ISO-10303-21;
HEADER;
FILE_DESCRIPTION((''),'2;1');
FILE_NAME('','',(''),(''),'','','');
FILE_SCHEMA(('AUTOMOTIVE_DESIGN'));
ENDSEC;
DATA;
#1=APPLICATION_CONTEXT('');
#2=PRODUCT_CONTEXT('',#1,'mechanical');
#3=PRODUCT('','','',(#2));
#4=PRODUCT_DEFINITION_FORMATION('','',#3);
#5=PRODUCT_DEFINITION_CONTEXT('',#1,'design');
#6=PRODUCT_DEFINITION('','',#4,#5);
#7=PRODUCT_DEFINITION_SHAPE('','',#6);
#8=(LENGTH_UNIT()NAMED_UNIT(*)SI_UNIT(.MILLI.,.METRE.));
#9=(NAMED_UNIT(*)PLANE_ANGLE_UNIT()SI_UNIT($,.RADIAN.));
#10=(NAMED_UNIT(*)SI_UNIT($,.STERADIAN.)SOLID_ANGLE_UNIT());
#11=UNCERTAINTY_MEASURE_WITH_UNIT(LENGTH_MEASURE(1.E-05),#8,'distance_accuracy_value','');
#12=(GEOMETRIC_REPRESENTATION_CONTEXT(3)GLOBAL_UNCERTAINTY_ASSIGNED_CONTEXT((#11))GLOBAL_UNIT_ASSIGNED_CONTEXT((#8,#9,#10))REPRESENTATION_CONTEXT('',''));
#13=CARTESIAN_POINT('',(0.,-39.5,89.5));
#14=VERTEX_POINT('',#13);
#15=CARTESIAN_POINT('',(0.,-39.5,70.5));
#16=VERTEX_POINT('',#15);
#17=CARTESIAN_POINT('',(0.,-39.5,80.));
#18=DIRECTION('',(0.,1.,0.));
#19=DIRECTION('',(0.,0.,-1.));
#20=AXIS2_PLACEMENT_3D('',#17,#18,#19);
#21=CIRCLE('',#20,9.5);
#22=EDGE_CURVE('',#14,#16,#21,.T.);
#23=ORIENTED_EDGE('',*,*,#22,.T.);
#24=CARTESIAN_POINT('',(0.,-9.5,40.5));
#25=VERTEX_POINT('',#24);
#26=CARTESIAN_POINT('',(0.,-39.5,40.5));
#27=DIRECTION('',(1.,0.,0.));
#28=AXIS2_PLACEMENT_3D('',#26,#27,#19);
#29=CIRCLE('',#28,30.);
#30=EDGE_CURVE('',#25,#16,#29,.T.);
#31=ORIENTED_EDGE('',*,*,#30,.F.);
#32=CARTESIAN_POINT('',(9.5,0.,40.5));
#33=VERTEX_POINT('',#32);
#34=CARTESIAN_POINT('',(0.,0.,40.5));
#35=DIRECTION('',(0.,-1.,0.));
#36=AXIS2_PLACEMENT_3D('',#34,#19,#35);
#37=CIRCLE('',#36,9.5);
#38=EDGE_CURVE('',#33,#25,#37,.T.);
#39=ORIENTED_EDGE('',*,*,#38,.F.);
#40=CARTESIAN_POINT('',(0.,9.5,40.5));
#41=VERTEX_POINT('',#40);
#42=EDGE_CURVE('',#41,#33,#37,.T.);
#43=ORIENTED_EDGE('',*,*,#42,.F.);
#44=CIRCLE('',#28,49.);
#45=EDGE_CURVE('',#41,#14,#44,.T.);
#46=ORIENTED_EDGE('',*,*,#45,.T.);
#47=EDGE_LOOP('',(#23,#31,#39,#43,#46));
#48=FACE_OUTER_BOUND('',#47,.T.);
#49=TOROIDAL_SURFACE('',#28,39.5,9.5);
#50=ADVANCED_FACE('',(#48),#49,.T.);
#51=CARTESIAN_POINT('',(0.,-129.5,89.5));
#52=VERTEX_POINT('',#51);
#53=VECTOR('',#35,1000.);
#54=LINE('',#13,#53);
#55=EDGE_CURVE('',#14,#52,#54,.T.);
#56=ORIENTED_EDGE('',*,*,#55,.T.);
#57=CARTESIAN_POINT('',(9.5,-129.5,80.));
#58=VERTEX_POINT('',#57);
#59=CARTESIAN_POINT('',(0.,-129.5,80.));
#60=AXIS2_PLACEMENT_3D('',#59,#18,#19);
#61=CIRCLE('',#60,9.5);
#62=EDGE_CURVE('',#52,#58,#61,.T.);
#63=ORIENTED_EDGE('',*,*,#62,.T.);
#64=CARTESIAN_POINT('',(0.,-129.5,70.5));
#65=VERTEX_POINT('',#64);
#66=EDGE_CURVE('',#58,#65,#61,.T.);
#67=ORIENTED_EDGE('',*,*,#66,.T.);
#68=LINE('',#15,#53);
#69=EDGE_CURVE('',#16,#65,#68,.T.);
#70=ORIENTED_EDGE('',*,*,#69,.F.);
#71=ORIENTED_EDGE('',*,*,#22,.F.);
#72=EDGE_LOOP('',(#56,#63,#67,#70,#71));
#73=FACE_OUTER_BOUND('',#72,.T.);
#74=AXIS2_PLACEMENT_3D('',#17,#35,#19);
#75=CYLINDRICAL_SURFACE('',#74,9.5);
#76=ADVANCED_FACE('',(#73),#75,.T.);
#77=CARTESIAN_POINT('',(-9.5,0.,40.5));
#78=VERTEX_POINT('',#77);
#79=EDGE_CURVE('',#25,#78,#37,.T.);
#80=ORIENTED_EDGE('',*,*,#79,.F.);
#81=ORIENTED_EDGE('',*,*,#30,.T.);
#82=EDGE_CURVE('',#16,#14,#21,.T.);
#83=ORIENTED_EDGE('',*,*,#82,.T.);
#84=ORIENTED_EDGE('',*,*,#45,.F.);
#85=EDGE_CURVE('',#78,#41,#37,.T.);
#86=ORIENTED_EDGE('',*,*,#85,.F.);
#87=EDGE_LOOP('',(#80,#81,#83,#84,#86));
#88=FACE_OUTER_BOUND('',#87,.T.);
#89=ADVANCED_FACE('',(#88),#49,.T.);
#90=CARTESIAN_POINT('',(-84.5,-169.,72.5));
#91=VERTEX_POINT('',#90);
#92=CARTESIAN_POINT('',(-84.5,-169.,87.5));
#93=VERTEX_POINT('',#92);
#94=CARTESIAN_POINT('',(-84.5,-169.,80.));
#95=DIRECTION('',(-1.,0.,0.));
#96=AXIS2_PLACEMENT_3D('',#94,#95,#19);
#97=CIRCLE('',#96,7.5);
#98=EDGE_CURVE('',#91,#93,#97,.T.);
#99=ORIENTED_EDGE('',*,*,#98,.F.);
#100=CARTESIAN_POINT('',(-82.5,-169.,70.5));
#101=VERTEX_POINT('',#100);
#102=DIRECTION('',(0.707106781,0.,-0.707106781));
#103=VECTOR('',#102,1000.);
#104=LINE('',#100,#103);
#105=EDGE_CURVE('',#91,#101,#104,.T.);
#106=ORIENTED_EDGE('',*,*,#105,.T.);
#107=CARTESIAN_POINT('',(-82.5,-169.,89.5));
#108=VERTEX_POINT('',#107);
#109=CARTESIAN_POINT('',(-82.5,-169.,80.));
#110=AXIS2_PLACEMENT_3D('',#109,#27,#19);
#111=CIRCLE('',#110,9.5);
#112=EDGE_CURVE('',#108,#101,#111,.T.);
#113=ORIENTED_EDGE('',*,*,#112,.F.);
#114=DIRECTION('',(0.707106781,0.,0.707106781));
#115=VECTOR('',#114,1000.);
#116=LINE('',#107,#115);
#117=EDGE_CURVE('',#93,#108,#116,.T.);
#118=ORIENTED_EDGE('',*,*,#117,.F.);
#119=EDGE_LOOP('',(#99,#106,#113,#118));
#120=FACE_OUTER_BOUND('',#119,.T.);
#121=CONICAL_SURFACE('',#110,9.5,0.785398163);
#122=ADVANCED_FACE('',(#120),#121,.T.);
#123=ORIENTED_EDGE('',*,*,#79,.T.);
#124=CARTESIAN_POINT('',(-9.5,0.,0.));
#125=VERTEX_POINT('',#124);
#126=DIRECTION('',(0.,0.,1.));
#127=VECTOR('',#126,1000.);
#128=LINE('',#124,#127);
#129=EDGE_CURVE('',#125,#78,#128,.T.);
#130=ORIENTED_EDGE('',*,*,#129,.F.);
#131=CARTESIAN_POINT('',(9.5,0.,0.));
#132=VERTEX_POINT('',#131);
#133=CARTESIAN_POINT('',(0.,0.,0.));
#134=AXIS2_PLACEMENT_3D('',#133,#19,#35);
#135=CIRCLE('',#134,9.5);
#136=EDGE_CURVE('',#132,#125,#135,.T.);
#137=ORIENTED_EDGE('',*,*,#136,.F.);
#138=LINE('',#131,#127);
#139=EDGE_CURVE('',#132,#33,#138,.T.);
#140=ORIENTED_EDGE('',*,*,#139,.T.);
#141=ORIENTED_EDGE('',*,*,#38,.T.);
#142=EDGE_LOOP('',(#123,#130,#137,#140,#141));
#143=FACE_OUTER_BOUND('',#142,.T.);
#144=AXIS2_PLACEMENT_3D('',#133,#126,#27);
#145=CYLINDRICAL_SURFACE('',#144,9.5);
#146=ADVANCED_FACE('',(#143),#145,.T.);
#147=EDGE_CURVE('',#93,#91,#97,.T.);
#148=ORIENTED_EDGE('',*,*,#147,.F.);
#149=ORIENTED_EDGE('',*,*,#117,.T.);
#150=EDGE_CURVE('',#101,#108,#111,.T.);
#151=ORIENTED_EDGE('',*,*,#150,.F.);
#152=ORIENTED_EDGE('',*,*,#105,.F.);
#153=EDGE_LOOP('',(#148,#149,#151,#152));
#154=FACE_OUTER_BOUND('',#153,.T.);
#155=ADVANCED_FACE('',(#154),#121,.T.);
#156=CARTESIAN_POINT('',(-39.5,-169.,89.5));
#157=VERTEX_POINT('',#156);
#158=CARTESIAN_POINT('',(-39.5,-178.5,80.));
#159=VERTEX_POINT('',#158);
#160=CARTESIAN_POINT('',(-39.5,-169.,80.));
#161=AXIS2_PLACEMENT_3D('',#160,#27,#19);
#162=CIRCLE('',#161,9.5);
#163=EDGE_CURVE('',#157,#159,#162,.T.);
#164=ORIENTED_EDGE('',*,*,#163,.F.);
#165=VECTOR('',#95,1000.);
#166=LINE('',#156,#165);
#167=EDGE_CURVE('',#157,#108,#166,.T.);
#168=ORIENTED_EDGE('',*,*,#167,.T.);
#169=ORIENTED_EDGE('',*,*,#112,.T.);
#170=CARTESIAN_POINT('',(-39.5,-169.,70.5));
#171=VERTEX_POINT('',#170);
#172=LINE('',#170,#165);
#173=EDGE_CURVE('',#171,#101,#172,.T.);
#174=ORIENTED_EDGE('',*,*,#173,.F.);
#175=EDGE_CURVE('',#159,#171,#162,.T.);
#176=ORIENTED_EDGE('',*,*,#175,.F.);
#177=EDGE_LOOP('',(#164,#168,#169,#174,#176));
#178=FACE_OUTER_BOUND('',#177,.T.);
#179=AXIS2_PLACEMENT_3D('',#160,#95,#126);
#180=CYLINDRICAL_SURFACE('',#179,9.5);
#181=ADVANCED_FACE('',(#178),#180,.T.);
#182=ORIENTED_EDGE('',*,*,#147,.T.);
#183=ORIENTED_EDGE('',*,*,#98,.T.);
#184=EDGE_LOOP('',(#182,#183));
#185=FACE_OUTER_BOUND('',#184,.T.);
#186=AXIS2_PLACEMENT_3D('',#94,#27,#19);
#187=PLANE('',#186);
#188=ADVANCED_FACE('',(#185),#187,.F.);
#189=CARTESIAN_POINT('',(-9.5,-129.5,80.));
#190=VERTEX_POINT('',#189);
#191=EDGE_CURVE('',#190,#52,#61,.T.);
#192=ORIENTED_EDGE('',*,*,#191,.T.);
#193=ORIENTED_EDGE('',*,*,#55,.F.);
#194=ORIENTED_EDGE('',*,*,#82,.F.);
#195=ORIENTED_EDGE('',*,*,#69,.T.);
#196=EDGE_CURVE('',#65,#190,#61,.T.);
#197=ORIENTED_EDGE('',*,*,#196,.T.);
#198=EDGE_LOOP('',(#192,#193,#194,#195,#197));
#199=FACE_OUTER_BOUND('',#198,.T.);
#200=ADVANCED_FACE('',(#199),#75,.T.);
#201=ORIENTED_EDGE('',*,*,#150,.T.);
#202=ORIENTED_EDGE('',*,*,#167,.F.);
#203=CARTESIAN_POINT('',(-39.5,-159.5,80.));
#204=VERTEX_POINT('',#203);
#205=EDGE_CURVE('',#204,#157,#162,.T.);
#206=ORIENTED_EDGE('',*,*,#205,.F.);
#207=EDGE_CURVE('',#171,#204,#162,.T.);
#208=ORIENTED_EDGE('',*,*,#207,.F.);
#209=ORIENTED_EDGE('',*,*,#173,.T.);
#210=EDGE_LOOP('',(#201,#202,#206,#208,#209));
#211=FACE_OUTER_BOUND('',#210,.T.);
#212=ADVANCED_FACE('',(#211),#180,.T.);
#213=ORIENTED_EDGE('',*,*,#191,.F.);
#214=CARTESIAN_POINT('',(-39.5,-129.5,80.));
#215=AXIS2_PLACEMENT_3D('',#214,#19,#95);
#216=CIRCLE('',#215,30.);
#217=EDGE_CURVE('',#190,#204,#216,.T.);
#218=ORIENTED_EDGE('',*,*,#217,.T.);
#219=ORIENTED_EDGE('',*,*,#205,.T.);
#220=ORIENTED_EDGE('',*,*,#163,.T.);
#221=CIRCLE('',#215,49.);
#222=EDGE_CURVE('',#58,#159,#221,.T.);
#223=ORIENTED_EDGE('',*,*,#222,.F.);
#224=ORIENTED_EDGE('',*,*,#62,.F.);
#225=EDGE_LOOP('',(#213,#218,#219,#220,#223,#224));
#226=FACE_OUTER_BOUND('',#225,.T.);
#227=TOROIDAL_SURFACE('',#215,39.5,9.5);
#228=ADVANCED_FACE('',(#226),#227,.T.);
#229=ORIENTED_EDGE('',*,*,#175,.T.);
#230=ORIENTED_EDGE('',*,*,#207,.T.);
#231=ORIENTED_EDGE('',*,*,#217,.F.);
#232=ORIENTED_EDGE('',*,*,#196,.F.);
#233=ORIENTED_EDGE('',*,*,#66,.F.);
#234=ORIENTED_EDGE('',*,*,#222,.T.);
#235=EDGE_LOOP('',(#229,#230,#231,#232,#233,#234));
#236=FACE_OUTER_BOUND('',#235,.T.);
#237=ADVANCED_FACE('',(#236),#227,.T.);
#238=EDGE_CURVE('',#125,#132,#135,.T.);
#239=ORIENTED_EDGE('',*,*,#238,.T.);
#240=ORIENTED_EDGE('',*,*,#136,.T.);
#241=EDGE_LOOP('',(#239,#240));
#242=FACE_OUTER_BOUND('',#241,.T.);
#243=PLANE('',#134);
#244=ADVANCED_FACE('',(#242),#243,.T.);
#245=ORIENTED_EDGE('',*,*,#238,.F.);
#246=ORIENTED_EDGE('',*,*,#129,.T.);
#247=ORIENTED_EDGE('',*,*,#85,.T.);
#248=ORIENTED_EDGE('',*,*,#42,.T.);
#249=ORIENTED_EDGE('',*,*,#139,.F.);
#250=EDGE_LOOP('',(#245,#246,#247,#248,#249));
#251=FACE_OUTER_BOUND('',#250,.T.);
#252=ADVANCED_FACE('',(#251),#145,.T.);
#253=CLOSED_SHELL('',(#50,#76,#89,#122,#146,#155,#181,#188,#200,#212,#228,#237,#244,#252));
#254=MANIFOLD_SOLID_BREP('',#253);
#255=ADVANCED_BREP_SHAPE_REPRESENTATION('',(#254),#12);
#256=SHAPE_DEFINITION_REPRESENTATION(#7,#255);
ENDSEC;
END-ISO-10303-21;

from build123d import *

# Parameters (mm, degrees)
SWEEP1_PROFILE_R = 9.5
CHAMFER1_SIZE    = 2


with BuildPart() as part:
    # Sweep1: sweep along a curve in space
    with BuildLine() as sweep1_path:
        Line((0, 0, 0), (0, 0, 40.5))
        ThreePointArc((0, 0, 40.5), (0, -11.569282143, 68.430717857), (0, -39.5, 80))
        Line((0, -39.5, 80), (0, -129.5, 80))
        ThreePointArc((0, -129.5, 80), (-11.569282143, -157.430717857, 80), (-39.5, -169, 80))
        Line((-39.5, -169, 80), (-84.5, -169, 80))
    # Sweep1 profile (on start of the path) → Sweep1 (sweep)
    with BuildSketch(Plane.XY):
        Circle(SWEEP1_PROFILE_R)
    sweep(path=sweep1_path.line)

    # Chamfer1
    chamfer1_edges = [part.edges().sort_by_distance(p)[0] for p in [
        (-84.5, -159.5, 80),
    ]]
    chamfer(chamfer1_edges, length=CHAMFER1_SIZE)


solid = part.part
